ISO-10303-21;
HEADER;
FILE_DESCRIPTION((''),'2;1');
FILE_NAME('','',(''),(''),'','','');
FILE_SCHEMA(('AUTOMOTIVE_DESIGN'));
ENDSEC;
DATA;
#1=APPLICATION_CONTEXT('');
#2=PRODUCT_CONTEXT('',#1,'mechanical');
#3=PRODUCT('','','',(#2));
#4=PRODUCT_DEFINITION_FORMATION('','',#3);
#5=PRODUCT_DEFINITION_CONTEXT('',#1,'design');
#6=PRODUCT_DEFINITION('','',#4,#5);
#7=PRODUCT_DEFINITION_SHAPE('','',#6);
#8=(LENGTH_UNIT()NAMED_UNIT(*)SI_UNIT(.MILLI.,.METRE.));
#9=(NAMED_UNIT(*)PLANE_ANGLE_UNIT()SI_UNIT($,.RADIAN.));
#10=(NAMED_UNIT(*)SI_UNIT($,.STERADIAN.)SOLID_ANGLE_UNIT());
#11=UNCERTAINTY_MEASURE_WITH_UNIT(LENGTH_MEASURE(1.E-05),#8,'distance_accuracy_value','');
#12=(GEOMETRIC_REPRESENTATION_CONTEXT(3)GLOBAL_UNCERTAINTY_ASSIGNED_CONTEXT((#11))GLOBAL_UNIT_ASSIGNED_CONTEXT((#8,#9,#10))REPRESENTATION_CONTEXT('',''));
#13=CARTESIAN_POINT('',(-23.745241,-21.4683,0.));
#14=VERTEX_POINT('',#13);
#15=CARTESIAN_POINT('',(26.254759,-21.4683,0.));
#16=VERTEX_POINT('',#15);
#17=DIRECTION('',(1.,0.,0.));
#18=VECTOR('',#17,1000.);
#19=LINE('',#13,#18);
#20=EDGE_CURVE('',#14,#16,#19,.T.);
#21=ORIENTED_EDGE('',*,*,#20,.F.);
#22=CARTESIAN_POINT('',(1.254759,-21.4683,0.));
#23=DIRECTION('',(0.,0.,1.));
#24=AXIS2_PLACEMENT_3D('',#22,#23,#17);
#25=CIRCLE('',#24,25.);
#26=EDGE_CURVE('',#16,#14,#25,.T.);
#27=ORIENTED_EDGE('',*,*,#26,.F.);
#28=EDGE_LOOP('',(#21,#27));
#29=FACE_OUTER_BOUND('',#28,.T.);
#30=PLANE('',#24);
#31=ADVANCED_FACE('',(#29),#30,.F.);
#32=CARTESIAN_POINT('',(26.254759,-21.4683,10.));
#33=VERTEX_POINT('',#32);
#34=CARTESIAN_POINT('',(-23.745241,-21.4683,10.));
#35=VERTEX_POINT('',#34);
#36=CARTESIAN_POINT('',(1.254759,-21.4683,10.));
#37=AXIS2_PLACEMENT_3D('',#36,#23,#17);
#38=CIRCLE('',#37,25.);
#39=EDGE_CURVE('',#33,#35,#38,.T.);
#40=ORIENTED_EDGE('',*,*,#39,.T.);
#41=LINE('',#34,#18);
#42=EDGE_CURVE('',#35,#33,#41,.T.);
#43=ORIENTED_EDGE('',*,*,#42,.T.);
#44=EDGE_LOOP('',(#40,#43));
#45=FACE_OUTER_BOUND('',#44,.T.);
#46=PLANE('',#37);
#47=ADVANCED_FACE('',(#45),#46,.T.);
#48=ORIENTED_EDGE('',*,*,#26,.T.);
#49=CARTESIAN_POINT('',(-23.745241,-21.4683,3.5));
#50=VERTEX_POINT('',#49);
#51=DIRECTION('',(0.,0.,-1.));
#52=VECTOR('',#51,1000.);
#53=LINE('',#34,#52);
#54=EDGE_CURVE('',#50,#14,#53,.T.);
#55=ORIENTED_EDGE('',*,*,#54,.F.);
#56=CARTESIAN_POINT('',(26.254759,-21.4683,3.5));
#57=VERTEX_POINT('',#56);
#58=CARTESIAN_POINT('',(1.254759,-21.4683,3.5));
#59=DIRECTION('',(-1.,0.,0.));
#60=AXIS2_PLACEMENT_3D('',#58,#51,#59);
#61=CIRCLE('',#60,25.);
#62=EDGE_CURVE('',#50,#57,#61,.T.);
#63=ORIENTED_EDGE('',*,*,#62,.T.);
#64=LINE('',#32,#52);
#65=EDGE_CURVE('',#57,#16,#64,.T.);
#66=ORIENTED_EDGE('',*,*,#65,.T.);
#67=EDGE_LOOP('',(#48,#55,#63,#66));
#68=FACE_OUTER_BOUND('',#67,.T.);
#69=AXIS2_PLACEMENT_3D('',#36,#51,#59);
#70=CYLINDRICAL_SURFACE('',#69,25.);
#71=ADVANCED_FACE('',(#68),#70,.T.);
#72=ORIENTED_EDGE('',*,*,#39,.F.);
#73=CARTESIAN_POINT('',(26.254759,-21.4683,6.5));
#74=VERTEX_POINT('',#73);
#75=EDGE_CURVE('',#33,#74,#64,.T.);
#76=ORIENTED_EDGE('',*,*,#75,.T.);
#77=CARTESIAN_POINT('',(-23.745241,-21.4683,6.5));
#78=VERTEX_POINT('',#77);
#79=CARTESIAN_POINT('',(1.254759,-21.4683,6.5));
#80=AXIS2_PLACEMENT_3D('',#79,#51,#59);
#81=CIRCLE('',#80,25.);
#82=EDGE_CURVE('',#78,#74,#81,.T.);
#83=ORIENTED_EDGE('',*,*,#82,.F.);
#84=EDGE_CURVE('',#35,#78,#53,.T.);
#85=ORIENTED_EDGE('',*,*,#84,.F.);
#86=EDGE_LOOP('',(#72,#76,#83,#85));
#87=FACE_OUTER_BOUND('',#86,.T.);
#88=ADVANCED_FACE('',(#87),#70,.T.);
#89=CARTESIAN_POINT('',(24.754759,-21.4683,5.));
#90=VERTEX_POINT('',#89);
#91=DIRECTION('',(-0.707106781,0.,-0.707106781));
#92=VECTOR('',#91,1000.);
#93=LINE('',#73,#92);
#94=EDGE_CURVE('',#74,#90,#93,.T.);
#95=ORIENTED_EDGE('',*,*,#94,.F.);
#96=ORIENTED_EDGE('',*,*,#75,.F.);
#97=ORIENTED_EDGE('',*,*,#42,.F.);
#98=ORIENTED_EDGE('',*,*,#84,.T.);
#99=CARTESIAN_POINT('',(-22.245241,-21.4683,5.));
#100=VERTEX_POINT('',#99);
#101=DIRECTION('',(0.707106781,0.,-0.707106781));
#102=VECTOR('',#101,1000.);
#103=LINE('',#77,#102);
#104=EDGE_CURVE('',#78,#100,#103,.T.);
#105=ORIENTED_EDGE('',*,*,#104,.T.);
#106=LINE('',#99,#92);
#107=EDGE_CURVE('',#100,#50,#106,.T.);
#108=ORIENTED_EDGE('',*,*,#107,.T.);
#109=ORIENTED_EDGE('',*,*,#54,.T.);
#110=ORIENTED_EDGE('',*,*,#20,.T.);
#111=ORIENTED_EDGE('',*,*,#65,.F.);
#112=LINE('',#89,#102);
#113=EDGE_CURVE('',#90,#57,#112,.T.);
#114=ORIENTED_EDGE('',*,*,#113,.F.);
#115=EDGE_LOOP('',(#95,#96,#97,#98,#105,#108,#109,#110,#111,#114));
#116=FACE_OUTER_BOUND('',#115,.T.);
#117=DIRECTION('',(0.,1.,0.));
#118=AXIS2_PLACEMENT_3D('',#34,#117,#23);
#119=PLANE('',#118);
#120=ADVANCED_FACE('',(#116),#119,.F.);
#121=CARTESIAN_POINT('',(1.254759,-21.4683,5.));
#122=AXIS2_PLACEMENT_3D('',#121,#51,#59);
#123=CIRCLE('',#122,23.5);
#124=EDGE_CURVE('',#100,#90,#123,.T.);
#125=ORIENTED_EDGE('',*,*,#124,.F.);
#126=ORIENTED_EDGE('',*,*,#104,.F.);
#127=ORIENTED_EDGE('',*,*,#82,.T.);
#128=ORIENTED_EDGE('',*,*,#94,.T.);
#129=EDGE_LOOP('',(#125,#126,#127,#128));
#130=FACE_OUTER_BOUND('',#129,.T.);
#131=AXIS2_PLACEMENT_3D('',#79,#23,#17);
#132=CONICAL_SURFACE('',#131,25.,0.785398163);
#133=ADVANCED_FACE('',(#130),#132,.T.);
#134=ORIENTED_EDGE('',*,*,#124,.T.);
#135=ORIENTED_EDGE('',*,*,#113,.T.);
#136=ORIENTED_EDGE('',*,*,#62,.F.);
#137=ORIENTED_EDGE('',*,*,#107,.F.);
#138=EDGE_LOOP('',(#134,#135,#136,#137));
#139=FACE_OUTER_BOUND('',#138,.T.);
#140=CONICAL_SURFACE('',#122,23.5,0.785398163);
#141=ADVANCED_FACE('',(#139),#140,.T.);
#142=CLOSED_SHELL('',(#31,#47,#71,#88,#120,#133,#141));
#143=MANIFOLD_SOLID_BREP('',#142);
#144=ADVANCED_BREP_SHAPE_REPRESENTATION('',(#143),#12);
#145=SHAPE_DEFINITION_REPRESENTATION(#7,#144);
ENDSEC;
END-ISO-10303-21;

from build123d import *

# Parameters (mm, degrees)
BOSS_EXTRUDE1_DEPTH = 10


with BuildPart() as part:
    # Sketch1 → Boss-Extrude1 (new body)
    with BuildSketch(Plane.XY):
        with BuildLine():
            Line((-23.745241043, -21.468300121), (26.254758957, -21.468300121))
            ThreePointArc((26.254758957, -21.468300121), (1.254758957, 3.531699879), (-23.745241043, -21.468300121))
        make_face()
    extrude(amount=BOSS_EXTRUDE1_DEPTH)

    # Cut-Sweep1: sweep along a path in Sketch4
    with BuildLine(Plane.XY.offset(5)) as cut_sweep1_path:
        ThreePointArc((26.254758957, -21.468300121), (1.254758957, 3.531699879), (-23.745241043, -21.468300121))
    # Sketch2 → Cut-Sweep1 (sweep, cut)
    with BuildSketch(Plane.XZ.offset(21.468300121)):
        Polygon((26.254758957, 5), (26.254758957, 6.5), (24.754758957, 5), (26.254758957, 3.5), align=None)
    sweep(path=cut_sweep1_path.line, mode=Mode.SUBTRACT)


solid = part.part
